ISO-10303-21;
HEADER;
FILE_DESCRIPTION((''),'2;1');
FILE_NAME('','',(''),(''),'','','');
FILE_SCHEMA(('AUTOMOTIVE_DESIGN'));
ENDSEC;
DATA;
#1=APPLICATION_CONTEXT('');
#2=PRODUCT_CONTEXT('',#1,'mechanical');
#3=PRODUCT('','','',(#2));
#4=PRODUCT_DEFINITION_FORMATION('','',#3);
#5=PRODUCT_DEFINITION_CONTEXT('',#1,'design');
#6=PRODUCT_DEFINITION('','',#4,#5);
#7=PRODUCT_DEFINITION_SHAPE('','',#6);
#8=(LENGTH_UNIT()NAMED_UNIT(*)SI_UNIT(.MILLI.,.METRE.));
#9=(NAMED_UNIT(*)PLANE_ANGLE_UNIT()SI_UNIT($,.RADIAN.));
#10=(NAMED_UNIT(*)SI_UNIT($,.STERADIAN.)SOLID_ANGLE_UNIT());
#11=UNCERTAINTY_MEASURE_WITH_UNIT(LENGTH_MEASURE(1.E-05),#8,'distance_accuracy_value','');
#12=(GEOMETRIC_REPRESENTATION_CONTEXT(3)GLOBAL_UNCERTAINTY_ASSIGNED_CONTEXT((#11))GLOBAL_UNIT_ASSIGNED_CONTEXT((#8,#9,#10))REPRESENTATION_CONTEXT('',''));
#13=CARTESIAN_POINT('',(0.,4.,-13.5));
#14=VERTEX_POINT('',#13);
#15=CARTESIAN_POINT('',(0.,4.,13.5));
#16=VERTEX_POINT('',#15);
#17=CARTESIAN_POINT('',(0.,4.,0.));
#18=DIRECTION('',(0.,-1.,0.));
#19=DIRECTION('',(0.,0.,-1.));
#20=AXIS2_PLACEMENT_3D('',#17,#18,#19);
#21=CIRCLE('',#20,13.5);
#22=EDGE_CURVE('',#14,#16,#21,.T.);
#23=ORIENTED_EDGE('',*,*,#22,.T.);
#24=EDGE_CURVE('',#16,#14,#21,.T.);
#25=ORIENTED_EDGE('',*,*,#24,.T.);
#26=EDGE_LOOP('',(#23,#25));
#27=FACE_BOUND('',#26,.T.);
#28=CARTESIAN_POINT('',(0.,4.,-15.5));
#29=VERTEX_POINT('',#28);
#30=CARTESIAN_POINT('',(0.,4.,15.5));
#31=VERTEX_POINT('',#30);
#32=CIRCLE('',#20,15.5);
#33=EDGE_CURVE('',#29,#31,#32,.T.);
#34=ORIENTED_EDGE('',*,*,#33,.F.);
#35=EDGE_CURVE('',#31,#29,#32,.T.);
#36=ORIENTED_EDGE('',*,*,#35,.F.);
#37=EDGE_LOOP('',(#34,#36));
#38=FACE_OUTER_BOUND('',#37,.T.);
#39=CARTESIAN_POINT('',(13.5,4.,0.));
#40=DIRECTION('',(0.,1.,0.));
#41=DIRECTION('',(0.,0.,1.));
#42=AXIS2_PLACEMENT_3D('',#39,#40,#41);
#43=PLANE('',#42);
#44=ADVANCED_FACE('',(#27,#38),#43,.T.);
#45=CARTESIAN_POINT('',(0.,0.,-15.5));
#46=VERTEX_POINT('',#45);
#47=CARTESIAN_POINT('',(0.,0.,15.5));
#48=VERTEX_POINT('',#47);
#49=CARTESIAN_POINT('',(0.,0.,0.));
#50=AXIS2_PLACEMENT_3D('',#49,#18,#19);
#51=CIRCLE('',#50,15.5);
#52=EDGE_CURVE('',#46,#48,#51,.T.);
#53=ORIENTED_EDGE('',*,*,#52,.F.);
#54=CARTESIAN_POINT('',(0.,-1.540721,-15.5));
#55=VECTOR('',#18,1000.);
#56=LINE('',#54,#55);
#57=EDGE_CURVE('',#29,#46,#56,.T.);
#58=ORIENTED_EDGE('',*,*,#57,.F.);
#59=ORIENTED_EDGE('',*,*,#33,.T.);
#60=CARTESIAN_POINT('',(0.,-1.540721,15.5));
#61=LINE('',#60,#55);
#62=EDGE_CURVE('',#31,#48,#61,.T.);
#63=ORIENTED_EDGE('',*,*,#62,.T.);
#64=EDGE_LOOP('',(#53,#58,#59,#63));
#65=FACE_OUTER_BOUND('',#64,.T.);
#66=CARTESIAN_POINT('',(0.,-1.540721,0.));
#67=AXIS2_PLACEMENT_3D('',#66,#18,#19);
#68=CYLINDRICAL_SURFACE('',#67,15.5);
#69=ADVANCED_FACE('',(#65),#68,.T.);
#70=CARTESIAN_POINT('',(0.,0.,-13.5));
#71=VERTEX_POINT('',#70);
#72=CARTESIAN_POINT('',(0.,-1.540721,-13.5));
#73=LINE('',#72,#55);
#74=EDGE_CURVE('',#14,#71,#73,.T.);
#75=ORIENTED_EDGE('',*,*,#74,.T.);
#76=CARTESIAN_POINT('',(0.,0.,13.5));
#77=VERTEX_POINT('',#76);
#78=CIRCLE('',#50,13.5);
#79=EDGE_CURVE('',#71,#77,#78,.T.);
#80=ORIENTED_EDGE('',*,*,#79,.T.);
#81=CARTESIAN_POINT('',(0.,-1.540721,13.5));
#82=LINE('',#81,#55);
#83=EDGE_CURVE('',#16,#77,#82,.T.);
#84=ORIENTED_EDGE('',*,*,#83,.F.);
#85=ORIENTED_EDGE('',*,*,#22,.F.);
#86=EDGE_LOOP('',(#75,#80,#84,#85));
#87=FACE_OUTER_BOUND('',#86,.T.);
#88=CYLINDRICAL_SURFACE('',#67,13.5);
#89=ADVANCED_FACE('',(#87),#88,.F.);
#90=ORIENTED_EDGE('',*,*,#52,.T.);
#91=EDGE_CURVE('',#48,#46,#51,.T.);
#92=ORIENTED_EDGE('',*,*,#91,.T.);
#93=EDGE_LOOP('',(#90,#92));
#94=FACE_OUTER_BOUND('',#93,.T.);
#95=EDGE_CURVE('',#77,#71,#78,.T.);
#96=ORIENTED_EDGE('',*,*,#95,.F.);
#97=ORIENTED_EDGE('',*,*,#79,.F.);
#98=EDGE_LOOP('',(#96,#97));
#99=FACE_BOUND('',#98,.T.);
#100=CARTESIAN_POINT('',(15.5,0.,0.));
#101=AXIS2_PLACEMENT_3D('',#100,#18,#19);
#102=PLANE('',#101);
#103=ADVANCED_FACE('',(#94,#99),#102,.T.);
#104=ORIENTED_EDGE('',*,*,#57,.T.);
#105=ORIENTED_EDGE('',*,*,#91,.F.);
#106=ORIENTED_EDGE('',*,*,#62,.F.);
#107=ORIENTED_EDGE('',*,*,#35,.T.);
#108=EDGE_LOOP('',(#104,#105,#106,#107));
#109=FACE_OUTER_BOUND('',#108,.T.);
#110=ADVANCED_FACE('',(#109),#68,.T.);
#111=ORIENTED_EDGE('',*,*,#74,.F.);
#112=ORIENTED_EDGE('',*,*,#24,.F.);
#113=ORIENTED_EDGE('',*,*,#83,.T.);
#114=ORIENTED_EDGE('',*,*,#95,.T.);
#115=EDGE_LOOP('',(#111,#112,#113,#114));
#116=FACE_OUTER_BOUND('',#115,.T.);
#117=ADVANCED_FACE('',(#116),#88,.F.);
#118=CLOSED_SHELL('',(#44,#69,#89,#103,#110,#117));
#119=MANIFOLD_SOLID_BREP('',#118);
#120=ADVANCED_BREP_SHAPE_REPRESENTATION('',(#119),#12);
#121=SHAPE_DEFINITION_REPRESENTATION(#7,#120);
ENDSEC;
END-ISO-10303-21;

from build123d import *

# Parameters (mm, degrees)
SKETCH2_W = 2
SKETCH2_H = 4


with BuildPart() as part:
    # Sketch2 → Revolve1 (revolve)
    with BuildSketch(Plane.XY, mode=Mode.PRIVATE) as revolve1_sk:
        with Locations((14.5, 2)):
            Rectangle(SKETCH2_W, SKETCH2_H)
    revolve(revolve1_sk.sketch.rotate(Axis((0, -1.540721456, 0), (0, 1, 0)), 90), axis=Axis((0, -1.540721456, 0), (0, 1, 0)))


solid = part.part
